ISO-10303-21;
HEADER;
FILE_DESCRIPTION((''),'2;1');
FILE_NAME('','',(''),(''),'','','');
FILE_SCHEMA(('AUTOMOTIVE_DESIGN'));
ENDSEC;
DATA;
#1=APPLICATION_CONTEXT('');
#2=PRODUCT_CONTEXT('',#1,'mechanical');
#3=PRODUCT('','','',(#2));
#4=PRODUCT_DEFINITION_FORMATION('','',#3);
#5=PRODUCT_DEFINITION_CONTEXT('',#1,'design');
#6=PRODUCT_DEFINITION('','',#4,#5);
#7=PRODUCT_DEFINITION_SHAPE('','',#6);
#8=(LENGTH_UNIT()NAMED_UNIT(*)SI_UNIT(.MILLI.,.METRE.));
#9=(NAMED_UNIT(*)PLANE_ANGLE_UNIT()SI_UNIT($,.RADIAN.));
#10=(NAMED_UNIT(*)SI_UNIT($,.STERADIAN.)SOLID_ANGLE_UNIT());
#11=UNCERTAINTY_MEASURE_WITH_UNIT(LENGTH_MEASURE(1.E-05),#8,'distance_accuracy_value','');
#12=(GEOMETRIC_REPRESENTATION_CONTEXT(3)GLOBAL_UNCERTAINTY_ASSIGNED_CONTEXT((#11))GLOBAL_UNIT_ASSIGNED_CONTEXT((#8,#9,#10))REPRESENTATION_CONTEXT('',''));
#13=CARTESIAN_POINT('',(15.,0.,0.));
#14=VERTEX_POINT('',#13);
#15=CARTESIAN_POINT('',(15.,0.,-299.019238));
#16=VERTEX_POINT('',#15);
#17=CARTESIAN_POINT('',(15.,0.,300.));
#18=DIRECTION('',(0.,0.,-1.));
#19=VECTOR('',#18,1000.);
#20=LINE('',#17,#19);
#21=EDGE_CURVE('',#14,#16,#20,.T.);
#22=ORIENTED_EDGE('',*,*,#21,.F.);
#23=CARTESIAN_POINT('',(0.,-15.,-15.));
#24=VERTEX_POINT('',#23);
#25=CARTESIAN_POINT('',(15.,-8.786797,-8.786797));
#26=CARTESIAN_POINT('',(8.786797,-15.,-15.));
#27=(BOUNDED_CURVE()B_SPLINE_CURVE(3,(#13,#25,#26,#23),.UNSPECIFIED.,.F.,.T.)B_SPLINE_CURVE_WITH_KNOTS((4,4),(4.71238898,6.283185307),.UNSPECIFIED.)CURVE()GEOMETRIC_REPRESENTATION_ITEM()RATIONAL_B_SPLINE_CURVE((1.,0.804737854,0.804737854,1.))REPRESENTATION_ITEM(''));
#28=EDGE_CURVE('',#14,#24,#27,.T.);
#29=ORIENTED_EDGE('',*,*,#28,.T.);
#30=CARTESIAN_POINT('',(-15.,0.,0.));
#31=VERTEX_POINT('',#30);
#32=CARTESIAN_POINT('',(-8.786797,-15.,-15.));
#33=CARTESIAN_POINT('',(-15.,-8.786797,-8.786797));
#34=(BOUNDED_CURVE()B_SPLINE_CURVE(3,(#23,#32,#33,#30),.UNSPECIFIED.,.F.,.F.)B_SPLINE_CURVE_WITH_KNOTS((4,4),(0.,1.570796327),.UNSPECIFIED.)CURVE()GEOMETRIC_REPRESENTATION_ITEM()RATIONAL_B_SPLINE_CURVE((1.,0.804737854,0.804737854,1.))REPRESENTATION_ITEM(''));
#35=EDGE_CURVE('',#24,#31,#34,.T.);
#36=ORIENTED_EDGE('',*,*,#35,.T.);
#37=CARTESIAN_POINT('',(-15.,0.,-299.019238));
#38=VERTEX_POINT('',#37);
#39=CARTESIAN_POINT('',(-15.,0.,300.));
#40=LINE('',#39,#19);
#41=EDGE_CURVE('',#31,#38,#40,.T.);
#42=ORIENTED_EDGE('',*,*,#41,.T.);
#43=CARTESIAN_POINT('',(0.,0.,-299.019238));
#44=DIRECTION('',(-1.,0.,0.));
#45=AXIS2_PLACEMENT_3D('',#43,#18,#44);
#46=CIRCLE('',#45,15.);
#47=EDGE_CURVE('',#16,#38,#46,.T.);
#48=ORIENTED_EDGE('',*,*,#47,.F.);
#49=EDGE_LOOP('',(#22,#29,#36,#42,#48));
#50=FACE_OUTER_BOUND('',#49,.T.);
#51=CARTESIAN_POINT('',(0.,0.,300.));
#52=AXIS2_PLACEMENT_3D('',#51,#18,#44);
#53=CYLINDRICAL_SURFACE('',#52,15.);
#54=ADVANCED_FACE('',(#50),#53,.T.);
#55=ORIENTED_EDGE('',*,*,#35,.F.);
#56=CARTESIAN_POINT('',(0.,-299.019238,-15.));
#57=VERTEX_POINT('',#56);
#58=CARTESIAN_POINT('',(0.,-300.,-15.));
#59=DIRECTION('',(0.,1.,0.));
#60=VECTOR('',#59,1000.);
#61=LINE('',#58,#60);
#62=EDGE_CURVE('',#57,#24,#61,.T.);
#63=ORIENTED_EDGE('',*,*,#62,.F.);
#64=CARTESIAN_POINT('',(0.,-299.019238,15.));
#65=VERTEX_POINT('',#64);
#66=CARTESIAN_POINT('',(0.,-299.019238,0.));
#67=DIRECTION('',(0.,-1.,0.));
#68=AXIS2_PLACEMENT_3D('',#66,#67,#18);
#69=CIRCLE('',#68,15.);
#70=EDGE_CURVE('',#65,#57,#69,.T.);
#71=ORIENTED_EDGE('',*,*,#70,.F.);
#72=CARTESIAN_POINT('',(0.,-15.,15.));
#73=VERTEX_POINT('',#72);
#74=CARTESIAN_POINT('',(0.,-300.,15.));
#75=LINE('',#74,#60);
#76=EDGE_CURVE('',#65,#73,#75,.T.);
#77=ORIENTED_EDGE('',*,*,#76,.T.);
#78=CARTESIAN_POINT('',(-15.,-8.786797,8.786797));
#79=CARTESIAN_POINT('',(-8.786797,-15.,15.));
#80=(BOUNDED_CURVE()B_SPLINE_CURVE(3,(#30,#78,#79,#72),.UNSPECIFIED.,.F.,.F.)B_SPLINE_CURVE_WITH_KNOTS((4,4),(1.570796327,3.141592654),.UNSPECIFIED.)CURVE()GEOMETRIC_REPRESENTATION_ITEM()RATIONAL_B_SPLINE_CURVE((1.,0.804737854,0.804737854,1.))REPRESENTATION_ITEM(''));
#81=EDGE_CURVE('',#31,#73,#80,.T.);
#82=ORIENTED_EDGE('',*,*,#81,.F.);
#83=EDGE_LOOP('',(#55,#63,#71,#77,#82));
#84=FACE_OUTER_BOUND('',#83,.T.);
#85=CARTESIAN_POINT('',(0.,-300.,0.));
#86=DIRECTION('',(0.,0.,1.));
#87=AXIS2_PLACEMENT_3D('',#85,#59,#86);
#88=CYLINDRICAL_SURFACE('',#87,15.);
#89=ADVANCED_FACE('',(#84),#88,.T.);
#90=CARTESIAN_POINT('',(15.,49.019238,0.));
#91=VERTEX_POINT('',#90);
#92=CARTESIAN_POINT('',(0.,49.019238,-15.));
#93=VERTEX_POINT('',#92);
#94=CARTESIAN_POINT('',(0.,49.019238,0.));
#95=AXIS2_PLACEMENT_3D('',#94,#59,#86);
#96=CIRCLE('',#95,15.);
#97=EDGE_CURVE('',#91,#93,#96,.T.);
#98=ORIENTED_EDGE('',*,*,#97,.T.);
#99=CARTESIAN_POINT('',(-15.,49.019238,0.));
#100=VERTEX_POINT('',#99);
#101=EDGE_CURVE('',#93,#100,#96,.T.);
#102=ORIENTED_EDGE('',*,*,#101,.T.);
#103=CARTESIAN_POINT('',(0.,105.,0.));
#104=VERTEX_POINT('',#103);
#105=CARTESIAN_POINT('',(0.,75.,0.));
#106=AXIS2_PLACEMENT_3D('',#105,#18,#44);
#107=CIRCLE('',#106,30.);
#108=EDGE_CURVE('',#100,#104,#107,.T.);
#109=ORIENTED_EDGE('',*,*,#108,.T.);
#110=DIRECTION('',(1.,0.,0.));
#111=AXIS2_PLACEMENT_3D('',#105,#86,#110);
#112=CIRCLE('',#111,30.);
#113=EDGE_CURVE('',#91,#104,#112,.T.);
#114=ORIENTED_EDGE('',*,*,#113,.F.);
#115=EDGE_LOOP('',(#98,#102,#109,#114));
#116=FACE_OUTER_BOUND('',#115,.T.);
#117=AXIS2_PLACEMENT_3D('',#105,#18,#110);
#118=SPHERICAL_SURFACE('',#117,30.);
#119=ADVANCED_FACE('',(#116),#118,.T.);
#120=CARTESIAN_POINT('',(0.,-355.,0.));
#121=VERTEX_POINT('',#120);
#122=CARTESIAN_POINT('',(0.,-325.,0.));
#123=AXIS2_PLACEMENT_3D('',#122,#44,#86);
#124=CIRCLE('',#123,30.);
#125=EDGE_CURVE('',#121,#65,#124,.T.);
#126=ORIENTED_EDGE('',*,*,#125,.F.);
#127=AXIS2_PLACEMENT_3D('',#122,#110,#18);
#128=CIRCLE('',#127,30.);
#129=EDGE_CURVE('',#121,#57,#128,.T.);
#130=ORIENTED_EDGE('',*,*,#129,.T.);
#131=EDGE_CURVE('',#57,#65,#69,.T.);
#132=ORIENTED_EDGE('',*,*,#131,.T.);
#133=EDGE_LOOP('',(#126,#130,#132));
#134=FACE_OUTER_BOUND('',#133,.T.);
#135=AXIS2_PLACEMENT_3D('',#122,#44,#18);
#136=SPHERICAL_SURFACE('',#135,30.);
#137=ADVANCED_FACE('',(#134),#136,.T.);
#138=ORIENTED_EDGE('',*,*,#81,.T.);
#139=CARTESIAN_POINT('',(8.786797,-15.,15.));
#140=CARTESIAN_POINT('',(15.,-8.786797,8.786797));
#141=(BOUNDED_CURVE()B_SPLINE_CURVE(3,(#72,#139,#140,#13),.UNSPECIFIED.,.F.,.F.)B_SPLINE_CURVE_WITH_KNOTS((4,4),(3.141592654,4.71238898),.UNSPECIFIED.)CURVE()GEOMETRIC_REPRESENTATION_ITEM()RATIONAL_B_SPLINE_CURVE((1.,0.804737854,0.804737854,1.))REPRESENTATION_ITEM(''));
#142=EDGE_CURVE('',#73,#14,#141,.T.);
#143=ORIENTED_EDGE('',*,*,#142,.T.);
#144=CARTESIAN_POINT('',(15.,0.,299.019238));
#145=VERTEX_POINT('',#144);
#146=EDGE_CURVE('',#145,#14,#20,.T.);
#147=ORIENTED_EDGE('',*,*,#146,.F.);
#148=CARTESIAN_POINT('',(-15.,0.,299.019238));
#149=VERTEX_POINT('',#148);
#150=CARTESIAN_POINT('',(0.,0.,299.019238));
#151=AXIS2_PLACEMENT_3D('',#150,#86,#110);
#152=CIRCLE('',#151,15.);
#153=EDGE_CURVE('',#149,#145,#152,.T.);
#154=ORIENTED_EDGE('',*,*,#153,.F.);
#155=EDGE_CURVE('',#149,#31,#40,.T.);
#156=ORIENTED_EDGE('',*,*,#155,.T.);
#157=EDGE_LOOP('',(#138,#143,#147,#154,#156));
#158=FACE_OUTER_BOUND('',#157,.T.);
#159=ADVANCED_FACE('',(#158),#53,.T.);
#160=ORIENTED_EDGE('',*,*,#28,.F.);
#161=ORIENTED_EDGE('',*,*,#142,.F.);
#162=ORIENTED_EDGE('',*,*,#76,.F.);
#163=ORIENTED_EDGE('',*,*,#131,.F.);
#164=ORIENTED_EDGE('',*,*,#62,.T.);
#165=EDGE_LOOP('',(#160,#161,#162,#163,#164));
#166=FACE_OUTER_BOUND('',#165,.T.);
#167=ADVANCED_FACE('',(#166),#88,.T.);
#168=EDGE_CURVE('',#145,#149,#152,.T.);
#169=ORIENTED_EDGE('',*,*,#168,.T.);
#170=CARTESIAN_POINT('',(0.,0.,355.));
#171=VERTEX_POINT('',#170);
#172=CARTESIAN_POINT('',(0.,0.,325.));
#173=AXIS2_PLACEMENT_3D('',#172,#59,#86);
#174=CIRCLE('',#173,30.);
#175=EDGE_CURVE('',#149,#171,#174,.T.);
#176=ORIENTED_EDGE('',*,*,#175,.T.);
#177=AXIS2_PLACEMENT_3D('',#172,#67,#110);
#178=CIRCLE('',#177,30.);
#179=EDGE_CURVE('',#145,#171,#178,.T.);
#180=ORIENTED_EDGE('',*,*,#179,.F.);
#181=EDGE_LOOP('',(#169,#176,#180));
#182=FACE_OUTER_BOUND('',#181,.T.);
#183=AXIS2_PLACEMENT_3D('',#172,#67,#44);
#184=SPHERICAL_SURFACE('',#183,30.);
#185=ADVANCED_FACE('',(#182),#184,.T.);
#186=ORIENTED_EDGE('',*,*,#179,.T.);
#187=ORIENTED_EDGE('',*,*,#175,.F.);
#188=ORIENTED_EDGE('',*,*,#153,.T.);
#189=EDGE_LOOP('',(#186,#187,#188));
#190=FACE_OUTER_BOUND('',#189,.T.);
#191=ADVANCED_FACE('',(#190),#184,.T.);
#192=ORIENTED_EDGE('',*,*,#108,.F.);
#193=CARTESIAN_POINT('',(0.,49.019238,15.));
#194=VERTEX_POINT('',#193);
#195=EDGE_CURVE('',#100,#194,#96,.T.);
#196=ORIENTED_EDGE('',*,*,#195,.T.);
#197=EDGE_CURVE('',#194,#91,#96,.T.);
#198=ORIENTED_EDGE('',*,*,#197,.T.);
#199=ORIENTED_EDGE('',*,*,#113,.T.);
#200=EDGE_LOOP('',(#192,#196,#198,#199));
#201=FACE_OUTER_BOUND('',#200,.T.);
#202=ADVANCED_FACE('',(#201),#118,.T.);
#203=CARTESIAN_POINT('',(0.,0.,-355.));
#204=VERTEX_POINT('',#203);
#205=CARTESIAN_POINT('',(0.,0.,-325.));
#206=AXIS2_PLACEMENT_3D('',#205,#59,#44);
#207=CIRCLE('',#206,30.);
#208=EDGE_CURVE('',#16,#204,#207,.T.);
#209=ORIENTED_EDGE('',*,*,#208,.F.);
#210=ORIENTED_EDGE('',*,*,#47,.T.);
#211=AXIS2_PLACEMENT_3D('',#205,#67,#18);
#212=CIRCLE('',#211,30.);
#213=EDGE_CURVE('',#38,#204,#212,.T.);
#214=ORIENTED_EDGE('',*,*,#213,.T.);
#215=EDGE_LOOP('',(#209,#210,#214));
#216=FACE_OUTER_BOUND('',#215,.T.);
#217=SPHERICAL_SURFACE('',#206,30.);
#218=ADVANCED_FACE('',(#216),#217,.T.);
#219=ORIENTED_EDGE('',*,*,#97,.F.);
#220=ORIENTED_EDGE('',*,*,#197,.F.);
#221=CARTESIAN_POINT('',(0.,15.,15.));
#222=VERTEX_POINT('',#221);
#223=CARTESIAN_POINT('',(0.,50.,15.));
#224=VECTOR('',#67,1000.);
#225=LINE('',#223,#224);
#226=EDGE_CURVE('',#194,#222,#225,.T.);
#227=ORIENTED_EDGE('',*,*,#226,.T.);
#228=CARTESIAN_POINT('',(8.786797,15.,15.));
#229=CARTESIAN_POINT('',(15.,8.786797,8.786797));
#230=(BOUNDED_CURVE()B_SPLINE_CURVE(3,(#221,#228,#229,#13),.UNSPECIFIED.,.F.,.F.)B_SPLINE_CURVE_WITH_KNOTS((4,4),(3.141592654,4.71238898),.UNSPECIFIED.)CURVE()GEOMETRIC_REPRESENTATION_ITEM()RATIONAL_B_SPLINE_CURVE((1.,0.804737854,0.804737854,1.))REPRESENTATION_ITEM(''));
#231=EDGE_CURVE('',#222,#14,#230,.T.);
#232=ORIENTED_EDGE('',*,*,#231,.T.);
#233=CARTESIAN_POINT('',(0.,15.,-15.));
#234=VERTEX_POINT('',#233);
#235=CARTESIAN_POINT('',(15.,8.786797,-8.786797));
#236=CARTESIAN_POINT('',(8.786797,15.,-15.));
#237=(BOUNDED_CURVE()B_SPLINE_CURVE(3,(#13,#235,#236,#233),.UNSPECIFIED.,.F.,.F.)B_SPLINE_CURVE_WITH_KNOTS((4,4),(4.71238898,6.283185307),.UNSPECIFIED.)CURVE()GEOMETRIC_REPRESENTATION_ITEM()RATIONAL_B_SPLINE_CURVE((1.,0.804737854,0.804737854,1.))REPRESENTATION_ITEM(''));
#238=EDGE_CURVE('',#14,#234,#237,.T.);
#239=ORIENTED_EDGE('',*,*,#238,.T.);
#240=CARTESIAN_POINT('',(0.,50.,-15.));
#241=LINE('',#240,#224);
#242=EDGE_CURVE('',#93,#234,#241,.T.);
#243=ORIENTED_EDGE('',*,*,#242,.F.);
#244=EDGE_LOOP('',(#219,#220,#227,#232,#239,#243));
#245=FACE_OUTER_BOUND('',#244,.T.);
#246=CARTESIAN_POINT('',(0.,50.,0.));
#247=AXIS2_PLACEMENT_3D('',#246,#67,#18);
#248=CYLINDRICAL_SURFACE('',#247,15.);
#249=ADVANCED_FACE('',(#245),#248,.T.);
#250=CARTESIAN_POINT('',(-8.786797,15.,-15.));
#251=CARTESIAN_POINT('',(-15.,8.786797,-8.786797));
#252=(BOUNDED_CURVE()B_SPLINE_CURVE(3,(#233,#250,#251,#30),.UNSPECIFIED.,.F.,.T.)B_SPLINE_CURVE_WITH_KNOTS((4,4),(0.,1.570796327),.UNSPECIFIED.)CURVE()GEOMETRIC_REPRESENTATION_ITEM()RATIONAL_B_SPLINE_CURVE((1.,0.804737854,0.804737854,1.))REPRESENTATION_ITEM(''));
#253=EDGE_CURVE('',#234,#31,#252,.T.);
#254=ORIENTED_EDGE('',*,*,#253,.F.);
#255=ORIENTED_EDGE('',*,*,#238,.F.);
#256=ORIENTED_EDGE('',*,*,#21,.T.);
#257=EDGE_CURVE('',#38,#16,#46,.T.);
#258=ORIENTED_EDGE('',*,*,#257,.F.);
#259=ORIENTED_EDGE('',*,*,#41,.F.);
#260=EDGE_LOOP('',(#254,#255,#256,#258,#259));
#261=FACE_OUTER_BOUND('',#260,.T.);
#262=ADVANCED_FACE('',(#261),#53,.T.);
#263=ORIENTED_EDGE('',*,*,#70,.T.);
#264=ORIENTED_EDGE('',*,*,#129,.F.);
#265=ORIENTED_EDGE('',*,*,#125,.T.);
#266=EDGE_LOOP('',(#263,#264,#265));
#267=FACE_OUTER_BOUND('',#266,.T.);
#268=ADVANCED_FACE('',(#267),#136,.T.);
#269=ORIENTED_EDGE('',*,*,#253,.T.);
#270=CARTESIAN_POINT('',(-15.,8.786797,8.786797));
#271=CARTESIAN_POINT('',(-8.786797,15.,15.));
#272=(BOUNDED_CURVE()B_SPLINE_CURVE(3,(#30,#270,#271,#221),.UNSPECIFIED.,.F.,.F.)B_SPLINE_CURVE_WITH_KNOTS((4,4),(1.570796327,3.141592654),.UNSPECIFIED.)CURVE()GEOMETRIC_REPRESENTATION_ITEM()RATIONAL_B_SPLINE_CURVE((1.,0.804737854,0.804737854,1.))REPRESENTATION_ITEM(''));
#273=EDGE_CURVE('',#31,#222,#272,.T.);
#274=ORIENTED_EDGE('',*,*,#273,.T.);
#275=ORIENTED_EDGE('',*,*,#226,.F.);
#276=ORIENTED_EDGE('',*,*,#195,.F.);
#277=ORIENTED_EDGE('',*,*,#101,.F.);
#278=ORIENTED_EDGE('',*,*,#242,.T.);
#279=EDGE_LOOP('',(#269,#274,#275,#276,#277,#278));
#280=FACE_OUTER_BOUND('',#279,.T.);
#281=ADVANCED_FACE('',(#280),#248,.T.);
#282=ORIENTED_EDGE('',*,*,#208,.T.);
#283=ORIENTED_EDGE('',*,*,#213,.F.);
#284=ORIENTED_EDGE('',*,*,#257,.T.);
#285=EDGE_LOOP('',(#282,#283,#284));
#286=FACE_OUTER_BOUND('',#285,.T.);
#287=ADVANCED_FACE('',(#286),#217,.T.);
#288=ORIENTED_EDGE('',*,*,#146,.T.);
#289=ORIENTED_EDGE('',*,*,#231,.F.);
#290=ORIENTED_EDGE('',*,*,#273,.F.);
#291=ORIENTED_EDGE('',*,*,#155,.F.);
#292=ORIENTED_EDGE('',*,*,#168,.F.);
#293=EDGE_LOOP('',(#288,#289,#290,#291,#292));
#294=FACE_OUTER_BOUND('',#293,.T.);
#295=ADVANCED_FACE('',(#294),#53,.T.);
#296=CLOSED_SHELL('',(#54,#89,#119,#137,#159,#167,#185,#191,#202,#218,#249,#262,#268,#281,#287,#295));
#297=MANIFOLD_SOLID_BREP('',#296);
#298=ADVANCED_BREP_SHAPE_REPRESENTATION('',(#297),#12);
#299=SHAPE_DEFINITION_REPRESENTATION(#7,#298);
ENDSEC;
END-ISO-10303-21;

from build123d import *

# Parameters (mm, degrees)
SKETCH1_R           = 15
BOSS_EXTRUDE1_DEPTH = 300
SKETCH3_R           = 15
BOSS_EXTRUDE2_DEPTH = 50
BOSS_EXTRUDE3_START = -300
SKETCH5_R           = 15
BOSS_EXTRUDE3_DEPTH = 300


with BuildPart() as part:
    # Sketch1 → Boss-Extrude1 (new, symmetric)
    with BuildSketch(Plane.XY):
        Circle(SKETCH1_R)
    extrude(amount=BOSS_EXTRUDE1_DEPTH, both=True)

    # Sketch2 → Revolve1 (revolve)
    with BuildSketch(Plane(origin=(0, 0, 0), x_dir=(1, 0, 0), z_dir=(0, 1, 0))):
        with BuildLine():
            Line((0, 355), (0, 295))
            ThreePointArc((0, 295), (30, 325), (0, 355))
        make_face()
    revolve1 = revolve(axis=Axis((0, 0, -355), (0, 0, 1)))

    # Mirror1: Revolve1 across plane
    add(revolve1.mirror(Plane.XY))

    # Sketch3 → Boss-Extrude2 (add)
    with BuildSketch(Plane(origin=(0, 0, 0), x_dir=(1, 0, 0), z_dir=(0, 1, 0))):
        Circle(SKETCH3_R)
    extrude(amount=BOSS_EXTRUDE2_DEPTH)

    # Sketch4 → Revolve2 (revolve)
    with BuildSketch(Plane.XY):
        with BuildLine():
            Line((0, 105), (0, 45))
            ThreePointArc((0, 45), (30, 75), (0, 105))
        make_face()
    revolve(axis=Axis((0, 105, 0), (0, -1, 0)))

    # Sketch5 → Boss-Extrude3 (add)
    with BuildSketch(Plane(origin=(0, 0, 0), x_dir=(1, 0, 0), z_dir=(0, 1, 0)).offset(BOSS_EXTRUDE3_START)):
        Circle(SKETCH5_R)
    extrude(amount=BOSS_EXTRUDE3_DEPTH)

    # Sketch6 → Revolve3 (revolve)
    with BuildSketch(Plane(origin=(0, 0, 0), x_dir=(0, 0, -1), z_dir=(1, 0, 0))):
        with BuildLine():
            Line((0, -295), (0, -355))
            ThreePointArc((0, -355), (-30, -325), (0, -295))
        make_face()
    revolve(axis=Axis((0, -295, 0), (0, -1, 0)))


solid = part.part
